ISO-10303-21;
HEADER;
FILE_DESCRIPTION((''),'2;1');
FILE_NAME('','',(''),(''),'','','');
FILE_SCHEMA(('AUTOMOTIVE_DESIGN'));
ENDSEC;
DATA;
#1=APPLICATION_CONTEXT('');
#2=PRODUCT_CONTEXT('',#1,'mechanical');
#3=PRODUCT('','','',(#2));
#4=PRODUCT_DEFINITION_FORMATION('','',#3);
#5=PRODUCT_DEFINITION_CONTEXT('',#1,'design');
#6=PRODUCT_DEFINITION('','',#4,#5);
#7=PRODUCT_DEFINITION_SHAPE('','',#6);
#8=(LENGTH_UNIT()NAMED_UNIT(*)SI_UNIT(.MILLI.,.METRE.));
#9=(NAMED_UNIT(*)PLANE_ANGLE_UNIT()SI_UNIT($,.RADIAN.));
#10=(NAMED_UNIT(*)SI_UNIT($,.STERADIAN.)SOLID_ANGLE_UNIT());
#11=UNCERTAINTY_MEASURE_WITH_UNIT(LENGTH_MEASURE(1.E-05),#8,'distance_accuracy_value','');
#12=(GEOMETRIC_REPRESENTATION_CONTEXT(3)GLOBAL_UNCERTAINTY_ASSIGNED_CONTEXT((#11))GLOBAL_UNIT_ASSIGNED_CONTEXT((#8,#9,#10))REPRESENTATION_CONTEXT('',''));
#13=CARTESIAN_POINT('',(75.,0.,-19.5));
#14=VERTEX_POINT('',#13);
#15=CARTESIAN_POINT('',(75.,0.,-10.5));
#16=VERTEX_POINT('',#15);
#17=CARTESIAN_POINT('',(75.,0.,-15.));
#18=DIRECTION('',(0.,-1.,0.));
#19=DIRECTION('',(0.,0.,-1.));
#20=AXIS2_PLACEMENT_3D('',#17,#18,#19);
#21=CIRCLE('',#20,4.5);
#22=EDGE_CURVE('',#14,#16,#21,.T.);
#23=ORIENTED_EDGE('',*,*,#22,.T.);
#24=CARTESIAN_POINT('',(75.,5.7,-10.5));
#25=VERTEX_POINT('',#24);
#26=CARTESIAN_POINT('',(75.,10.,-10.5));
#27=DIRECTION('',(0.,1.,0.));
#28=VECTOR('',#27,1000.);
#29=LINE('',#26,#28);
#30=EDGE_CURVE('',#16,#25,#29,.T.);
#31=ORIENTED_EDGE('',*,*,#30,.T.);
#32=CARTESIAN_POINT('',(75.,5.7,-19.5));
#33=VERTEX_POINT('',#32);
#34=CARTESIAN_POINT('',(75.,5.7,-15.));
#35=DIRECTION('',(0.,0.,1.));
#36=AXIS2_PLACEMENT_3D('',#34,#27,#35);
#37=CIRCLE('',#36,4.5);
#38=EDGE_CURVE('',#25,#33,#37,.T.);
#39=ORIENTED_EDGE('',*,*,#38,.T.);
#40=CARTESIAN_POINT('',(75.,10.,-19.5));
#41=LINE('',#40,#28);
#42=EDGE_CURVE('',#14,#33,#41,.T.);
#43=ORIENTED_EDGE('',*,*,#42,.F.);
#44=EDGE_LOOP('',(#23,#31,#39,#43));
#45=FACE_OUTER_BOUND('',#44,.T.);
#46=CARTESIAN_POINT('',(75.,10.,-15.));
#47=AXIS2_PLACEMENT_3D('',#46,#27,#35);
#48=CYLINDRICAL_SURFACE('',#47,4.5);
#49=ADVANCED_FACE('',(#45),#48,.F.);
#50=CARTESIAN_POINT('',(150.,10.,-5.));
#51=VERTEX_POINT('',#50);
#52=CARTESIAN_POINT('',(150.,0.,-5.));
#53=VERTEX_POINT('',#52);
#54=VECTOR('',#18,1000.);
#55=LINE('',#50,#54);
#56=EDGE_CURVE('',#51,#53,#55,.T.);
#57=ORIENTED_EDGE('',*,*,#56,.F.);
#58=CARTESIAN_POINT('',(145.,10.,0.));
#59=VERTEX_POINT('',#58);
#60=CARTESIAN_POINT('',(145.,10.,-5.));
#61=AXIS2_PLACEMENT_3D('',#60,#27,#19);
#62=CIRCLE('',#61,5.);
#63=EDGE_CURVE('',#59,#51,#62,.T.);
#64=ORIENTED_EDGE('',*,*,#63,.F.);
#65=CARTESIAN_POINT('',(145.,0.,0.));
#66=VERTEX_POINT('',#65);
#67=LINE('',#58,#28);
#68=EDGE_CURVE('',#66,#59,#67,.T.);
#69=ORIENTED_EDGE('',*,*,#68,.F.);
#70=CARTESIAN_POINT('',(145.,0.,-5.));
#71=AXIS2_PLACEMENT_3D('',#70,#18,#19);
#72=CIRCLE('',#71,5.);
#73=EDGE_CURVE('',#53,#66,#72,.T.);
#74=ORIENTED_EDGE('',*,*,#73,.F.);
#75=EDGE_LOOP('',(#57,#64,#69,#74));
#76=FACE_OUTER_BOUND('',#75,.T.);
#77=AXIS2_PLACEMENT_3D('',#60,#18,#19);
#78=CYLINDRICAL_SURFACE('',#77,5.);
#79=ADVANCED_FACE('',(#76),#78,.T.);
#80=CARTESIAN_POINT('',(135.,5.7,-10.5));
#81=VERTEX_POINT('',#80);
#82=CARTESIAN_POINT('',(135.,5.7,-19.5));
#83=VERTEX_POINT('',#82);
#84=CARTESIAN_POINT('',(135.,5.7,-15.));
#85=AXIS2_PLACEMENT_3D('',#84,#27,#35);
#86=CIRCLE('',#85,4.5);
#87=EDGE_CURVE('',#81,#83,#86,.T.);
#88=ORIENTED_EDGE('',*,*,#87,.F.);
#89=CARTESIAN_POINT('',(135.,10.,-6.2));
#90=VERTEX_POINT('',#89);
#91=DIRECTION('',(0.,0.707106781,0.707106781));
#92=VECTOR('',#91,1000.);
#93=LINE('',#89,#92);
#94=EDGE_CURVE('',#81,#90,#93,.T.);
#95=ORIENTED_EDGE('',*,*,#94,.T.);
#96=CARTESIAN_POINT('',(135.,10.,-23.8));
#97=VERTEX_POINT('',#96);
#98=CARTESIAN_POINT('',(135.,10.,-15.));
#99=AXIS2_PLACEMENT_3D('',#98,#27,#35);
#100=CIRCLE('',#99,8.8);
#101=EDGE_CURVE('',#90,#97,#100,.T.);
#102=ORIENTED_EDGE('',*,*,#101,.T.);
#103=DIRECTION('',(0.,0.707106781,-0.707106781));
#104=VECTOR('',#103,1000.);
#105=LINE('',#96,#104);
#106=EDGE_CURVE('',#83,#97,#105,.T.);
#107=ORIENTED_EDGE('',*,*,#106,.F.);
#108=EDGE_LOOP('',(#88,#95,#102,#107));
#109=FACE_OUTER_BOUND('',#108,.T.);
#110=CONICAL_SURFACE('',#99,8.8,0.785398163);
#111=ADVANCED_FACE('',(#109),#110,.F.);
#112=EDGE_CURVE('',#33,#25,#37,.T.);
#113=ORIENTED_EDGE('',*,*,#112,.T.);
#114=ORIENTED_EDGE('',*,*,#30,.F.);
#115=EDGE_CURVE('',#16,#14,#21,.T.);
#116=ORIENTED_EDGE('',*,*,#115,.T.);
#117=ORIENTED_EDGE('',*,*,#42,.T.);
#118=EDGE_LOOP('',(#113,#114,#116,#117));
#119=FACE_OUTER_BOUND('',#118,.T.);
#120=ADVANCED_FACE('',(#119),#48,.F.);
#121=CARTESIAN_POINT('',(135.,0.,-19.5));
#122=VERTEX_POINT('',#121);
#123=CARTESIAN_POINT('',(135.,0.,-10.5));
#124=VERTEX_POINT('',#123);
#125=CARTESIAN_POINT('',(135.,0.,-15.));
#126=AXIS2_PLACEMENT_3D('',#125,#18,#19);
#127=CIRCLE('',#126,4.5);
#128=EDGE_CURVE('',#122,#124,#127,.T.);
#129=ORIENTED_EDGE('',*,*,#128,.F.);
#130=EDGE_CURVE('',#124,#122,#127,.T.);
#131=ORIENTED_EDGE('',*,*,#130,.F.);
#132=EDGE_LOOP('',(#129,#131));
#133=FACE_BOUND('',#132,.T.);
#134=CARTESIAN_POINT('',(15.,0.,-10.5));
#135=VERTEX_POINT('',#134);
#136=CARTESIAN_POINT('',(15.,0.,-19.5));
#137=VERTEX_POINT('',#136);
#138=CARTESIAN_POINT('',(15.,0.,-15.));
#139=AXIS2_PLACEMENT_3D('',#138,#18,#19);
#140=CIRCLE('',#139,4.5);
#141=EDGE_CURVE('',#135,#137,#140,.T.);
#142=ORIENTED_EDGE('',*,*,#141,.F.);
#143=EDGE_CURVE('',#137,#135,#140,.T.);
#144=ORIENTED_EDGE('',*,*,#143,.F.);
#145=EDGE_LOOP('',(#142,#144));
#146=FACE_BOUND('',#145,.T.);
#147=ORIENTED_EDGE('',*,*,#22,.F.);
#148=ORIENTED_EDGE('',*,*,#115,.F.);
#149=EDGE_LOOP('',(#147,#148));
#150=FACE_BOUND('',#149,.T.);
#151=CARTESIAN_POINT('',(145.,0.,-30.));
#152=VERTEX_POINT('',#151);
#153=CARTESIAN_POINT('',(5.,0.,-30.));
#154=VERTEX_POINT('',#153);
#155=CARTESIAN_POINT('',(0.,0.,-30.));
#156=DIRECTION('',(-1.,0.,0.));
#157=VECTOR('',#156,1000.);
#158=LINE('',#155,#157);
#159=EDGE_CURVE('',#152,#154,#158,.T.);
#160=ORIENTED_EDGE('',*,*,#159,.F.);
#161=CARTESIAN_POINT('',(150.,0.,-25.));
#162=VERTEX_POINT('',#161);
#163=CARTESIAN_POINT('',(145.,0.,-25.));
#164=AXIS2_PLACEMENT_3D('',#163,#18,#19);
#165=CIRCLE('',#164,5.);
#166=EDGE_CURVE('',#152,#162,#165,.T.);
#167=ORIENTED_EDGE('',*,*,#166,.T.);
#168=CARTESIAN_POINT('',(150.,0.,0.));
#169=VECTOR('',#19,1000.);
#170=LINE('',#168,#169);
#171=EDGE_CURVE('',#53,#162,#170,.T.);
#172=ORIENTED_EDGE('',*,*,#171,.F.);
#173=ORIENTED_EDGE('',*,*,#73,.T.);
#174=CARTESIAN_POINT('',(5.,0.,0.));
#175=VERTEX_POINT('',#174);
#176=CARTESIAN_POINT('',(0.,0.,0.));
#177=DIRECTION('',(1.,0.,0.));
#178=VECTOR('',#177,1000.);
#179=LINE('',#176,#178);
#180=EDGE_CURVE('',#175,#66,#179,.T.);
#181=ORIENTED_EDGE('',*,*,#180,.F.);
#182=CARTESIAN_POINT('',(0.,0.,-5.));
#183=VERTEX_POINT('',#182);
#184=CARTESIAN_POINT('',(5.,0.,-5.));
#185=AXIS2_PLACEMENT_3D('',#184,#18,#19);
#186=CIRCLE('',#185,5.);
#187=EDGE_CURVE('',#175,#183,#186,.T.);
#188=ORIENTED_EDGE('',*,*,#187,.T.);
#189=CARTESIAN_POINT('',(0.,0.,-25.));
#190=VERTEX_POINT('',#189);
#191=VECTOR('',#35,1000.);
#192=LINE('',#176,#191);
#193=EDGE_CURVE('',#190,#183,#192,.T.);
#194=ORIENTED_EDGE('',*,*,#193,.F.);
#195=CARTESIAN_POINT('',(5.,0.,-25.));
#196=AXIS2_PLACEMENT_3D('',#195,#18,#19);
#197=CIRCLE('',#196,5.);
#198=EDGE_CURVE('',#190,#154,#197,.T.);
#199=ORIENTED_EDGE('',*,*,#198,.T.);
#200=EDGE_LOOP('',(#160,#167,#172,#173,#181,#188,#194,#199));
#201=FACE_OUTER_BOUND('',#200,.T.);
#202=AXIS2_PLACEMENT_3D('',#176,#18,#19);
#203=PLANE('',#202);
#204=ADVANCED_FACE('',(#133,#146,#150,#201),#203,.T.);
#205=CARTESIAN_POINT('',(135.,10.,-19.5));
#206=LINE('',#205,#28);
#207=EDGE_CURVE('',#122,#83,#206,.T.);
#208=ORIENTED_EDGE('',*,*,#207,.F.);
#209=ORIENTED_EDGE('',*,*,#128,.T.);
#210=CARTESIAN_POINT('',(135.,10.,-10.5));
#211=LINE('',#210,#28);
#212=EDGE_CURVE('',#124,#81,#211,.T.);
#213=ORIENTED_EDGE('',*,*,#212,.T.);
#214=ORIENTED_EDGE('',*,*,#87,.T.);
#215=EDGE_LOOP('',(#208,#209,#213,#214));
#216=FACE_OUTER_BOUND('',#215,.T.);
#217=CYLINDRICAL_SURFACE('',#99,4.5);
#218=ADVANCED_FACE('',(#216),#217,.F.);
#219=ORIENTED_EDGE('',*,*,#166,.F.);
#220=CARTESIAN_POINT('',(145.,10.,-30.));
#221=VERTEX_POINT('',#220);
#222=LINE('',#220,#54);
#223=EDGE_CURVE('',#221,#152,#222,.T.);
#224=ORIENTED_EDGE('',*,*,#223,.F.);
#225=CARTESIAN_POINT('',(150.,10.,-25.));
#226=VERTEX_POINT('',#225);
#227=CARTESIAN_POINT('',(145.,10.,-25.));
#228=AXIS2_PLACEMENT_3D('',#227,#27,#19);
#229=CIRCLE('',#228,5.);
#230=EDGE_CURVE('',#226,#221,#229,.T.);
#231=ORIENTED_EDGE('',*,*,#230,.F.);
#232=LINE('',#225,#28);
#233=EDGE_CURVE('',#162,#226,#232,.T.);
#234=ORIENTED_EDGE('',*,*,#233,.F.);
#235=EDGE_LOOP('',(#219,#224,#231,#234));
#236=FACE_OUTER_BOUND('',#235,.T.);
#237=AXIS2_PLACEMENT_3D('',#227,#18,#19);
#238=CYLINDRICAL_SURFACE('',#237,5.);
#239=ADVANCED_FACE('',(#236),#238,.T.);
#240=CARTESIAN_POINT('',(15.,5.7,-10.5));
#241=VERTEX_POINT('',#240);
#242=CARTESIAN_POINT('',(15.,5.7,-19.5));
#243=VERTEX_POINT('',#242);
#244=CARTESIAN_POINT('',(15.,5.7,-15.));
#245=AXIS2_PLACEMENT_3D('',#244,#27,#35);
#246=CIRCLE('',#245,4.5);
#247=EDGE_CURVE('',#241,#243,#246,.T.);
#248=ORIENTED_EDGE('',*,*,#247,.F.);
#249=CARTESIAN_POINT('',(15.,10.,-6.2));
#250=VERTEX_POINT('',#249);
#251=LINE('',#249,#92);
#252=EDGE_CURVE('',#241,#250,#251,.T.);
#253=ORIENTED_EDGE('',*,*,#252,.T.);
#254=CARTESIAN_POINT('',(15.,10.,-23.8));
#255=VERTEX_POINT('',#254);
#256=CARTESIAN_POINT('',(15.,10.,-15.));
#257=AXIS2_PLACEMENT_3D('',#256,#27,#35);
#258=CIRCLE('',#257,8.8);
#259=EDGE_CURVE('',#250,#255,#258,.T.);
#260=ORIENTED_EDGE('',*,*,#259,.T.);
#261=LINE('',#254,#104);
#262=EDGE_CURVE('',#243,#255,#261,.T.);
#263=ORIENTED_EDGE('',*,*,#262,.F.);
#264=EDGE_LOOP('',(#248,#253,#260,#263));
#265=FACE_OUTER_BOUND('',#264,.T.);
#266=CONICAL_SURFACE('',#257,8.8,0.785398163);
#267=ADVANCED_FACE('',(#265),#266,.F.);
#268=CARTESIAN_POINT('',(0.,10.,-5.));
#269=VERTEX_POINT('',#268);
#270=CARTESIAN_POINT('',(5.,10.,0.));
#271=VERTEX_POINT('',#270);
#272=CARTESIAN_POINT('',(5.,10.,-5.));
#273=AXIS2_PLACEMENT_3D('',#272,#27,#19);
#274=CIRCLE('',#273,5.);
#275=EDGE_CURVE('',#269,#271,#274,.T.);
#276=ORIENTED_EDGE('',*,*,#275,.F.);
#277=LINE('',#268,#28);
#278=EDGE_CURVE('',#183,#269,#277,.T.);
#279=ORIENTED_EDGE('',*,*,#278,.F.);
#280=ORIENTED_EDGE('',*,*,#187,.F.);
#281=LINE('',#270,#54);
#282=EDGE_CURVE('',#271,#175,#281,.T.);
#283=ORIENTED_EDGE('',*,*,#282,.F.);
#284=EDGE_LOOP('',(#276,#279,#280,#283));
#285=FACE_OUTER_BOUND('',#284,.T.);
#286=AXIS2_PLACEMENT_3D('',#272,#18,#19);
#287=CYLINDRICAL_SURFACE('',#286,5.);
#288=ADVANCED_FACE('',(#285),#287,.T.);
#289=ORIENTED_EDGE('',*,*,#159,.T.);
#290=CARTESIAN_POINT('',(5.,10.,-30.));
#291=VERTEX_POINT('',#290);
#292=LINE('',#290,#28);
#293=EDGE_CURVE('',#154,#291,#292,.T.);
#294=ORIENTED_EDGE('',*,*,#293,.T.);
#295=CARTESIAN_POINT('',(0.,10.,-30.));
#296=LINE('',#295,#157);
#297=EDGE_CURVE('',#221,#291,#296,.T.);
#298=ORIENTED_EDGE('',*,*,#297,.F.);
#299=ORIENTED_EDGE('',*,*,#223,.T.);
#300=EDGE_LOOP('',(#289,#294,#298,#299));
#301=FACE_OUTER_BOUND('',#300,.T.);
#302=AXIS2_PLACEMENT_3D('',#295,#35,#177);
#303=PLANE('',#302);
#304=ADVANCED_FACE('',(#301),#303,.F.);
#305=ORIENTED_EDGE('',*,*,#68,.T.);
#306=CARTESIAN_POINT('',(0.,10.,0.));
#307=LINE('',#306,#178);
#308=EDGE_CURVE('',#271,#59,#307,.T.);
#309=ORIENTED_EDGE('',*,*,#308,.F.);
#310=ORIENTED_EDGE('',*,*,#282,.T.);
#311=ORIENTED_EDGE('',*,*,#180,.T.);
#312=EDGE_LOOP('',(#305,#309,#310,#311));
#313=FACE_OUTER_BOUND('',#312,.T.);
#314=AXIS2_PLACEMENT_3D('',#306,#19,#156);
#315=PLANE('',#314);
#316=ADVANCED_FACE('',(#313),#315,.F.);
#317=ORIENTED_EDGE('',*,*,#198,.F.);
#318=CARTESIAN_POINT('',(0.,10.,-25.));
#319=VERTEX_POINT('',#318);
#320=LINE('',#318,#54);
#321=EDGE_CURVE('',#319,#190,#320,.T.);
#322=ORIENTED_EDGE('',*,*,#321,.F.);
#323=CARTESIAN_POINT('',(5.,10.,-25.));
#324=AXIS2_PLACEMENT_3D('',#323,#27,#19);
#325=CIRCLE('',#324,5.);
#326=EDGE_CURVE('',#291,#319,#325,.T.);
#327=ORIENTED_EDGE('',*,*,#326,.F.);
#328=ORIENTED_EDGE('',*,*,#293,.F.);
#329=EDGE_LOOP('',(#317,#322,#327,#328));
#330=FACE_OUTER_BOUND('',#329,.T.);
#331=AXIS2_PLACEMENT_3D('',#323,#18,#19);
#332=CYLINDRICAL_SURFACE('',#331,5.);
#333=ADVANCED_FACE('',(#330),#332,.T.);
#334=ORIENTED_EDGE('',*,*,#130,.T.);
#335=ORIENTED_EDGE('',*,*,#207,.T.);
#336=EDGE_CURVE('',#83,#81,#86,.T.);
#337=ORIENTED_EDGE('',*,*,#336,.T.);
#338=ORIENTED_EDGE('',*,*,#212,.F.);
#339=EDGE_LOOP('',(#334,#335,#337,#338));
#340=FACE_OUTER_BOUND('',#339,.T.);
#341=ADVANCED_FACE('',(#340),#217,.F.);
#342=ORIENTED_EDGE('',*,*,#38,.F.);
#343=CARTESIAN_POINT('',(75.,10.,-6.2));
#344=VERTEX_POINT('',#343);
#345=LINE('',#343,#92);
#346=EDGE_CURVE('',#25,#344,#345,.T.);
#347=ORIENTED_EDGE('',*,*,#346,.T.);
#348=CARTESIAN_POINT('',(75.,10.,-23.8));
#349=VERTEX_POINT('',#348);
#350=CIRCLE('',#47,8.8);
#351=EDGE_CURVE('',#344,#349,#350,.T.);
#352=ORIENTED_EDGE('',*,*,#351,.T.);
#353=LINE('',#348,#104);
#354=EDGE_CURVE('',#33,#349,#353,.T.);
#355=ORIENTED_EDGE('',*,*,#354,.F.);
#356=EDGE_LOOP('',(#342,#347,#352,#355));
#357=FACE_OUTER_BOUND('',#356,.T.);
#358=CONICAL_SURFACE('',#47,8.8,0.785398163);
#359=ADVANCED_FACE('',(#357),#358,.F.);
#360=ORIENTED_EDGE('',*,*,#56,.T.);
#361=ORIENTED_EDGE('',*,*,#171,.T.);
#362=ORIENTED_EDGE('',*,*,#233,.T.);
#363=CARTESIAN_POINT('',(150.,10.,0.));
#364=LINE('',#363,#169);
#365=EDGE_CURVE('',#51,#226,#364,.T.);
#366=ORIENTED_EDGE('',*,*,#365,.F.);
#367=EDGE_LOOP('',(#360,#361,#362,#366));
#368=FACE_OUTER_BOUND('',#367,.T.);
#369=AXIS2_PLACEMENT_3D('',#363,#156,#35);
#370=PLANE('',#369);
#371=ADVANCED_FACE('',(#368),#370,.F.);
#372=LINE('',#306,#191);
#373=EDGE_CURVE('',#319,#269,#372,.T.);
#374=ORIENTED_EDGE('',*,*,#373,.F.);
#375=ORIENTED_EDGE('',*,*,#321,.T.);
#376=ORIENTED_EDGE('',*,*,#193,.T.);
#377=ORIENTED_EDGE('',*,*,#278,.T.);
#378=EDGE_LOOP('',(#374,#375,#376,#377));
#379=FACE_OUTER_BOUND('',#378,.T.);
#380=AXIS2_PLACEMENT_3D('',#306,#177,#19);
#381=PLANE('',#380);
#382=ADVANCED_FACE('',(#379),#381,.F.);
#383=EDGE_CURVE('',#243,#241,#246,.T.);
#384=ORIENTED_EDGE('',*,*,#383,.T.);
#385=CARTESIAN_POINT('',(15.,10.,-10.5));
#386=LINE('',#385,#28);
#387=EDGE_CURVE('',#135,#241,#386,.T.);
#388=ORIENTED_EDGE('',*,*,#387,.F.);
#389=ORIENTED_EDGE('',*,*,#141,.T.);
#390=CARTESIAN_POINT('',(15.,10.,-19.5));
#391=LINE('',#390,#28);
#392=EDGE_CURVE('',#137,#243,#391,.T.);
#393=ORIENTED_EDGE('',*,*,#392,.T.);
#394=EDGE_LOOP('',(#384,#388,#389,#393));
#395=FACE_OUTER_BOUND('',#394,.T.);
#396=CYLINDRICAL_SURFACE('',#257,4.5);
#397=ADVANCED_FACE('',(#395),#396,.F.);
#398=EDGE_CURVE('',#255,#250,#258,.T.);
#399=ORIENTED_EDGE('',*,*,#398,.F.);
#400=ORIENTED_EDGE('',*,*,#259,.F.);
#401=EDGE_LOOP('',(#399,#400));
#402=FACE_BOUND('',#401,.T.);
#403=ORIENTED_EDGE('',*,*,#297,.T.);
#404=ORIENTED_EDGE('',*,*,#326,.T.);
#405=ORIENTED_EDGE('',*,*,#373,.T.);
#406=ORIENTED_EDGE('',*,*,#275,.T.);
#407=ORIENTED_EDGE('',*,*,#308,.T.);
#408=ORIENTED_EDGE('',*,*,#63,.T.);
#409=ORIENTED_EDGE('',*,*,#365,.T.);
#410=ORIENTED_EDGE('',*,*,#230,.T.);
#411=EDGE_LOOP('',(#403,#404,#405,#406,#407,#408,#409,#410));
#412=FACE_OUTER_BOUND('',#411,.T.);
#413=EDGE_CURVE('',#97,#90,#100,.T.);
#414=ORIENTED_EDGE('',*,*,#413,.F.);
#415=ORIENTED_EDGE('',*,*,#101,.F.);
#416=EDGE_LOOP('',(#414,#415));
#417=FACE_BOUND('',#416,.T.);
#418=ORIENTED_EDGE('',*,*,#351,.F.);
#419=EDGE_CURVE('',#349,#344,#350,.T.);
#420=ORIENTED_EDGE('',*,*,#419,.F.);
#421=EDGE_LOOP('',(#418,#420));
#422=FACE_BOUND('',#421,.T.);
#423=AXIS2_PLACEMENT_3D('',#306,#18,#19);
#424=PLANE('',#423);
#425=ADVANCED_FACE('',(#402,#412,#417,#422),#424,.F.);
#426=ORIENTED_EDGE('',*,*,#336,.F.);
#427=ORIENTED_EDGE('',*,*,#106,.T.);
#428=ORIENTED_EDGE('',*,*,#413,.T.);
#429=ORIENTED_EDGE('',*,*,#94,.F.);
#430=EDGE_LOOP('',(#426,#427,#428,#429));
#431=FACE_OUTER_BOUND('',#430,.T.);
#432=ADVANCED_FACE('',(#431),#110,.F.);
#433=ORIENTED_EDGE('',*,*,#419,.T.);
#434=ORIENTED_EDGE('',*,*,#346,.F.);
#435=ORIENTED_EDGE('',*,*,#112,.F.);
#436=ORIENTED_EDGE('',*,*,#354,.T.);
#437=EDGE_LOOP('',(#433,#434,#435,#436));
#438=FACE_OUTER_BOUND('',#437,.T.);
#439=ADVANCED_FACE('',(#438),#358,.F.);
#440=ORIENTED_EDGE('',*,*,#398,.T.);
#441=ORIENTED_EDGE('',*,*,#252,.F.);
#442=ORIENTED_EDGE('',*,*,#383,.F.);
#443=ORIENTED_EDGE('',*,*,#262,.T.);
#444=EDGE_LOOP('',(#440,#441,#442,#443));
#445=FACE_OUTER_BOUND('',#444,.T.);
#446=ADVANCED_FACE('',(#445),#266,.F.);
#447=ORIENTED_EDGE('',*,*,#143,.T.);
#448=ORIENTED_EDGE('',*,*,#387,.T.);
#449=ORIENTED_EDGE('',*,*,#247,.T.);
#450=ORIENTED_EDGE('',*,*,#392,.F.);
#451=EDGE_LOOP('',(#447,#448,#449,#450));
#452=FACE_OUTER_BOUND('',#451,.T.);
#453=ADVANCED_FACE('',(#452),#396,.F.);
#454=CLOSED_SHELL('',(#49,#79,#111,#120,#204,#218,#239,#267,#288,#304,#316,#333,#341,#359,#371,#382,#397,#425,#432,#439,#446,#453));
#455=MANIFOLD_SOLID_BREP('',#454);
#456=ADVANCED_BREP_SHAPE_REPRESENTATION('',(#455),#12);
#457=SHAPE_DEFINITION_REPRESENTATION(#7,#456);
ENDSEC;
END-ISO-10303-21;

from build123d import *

# Parameters (mm, degrees)
SKETCH1_W                                  = 150
SKETCH1_H                                  = 30
BOSS_EXTRUDE1_DEPTH                        = 10
FILLET1_R                                  = 5
SOCKET_BUTTON_HEAD_SCREW_HOLE1_D           = 9
SOCKET_BUTTON_HEAD_SCREW_HOLE1_DEPTH       = 19.75
SOCKET_BUTTON_HEAD_SCREW_HOLE1_CSINK_D     = 17.6
SOCKET_BUTTON_HEAD_SCREW_HOLE1_CSINK_ANGLE = 90
SOCKET_BUTTON_HEAD_SCREW_HOLE1_TIP         = 2.703872786


with BuildPart() as part:
    # Sketch1 → Boss-Extrude1 (new body)
    with BuildSketch(Plane(origin=(0, 0, 0), x_dir=(1, 0, 0), z_dir=(0, 1, 0))):
        with Locations((75, 15)):
            Rectangle(SKETCH1_W, SKETCH1_H)
    extrude(amount=BOSS_EXTRUDE1_DEPTH)

    # Fillet1
    fillet1_edges = [part.edges().sort_by_distance(p)[0] for p in [
        (0, 5, -30),
        (150, 5, -30),
        (150, 5, 0),
        (0, 5, 0),
    ]]
    fillet(fillet1_edges, radius=FILLET1_R)

    # Socket Button Head Screw Hole1
    with Locations(Plane(origin=(0, 10, 0), x_dir=(1, 0, 0), z_dir=(0, 1, 0))):
        with Locations((75, 15), (15, 15), (135, 15)):
            CounterSinkHole(SOCKET_BUTTON_HEAD_SCREW_HOLE1_D / 2, SOCKET_BUTTON_HEAD_SCREW_HOLE1_CSINK_D / 2, depth=SOCKET_BUTTON_HEAD_SCREW_HOLE1_DEPTH, counter_sink_angle=SOCKET_BUTTON_HEAD_SCREW_HOLE1_CSINK_ANGLE)
            with Locations((0, 0, -(SOCKET_BUTTON_HEAD_SCREW_HOLE1_DEPTH + SOCKET_BUTTON_HEAD_SCREW_HOLE1_TIP / 2))):  # 118° drill point
                Cone(0, SOCKET_BUTTON_HEAD_SCREW_HOLE1_D / 2, SOCKET_BUTTON_HEAD_SCREW_HOLE1_TIP, mode=Mode.SUBTRACT)


solid = part.part
